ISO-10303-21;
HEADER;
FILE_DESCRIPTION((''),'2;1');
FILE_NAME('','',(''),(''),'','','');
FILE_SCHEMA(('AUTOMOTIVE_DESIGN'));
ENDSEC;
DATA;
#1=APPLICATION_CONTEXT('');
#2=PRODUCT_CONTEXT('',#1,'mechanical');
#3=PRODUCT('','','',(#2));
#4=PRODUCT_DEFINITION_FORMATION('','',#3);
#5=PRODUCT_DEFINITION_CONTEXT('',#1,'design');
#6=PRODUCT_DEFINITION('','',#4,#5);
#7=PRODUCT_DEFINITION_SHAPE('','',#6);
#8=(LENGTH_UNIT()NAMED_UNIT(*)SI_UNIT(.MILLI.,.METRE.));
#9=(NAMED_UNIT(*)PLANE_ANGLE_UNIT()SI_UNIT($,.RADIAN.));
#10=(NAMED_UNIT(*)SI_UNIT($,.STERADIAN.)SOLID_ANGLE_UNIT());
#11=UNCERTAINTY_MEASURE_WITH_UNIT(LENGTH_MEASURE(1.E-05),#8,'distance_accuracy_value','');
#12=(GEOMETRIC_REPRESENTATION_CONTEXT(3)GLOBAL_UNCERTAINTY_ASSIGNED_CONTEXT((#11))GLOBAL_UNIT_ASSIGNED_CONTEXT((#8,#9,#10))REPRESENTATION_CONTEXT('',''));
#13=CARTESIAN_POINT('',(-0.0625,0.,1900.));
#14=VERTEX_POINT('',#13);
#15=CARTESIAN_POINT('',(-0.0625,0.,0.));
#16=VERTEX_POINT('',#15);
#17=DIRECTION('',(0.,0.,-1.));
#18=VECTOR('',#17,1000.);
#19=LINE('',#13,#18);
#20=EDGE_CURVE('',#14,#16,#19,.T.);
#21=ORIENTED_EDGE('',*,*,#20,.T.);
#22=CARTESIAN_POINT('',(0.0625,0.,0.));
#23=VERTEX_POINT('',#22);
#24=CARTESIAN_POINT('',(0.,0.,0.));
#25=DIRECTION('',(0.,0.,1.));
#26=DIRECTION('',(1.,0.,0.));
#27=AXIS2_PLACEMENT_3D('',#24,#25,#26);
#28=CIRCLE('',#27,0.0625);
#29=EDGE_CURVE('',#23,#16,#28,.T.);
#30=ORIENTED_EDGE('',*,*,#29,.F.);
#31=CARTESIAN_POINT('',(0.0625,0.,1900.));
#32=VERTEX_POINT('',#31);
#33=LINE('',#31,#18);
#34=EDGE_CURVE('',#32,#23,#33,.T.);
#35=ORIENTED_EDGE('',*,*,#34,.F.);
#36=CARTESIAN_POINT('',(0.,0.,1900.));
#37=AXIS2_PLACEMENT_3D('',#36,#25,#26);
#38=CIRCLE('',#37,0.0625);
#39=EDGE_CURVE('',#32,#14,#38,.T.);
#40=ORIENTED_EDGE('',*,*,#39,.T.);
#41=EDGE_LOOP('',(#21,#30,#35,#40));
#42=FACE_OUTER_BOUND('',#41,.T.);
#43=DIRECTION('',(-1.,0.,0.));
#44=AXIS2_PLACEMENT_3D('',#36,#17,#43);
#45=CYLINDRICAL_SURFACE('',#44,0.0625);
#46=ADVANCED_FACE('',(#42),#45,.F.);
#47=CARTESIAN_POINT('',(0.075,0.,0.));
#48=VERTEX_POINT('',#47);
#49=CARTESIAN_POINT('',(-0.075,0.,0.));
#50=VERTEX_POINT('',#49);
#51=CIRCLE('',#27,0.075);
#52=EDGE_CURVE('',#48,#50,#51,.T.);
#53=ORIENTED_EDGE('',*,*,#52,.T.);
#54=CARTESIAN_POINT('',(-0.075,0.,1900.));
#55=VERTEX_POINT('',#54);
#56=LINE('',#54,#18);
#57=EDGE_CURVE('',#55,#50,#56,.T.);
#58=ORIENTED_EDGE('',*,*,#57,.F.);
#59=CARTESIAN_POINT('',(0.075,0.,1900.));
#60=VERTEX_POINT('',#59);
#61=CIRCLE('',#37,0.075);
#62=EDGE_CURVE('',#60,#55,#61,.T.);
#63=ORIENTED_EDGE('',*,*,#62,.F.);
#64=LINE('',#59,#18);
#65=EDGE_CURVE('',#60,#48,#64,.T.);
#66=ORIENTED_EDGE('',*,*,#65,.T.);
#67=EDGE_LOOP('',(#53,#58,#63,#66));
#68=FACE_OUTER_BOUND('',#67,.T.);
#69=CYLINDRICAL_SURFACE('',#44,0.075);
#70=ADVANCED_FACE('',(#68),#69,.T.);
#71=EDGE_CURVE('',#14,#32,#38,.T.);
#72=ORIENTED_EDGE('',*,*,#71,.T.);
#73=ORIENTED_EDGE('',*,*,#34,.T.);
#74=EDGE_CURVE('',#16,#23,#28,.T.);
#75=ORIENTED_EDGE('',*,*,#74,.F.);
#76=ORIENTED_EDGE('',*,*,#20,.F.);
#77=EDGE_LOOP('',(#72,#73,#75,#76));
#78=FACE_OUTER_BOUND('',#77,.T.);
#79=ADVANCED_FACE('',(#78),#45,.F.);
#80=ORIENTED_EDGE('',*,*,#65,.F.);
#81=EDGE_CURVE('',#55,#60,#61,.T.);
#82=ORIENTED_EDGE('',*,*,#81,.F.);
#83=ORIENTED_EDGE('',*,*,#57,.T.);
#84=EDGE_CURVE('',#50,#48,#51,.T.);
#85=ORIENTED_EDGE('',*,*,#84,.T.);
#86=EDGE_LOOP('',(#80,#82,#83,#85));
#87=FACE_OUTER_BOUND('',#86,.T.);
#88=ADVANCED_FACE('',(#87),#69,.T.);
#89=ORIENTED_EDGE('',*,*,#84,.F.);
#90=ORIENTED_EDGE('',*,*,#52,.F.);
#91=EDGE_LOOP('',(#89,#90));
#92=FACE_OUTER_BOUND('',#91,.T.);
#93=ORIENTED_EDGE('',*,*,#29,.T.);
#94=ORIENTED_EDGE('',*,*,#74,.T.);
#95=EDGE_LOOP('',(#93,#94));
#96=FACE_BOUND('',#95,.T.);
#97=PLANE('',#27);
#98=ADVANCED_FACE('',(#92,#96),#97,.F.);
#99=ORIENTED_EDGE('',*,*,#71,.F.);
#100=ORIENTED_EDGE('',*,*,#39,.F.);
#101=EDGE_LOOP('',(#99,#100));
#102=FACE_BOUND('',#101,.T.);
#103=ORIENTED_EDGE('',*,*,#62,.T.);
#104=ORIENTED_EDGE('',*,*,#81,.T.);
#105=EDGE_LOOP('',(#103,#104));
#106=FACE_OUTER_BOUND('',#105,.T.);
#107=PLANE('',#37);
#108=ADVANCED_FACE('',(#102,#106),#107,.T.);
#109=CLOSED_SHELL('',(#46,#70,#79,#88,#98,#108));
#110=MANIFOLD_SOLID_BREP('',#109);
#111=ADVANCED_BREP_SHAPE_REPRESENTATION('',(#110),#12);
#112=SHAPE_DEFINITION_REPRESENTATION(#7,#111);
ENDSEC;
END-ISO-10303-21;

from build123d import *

# Parameters (mm, degrees)
SKETCH1_R           = 0.075
SKETCH1_R_2         = 0.0625
BOSS_EXTRUDE1_DEPTH = 1900


with BuildPart() as part:
    # Sketch1 → Boss-Extrude1 (new body)
    with BuildSketch(Plane.XY):
        Circle(SKETCH1_R)
        Circle(SKETCH1_R_2, mode=Mode.SUBTRACT)
    extrude(amount=BOSS_EXTRUDE1_DEPTH)


solid = part.part
